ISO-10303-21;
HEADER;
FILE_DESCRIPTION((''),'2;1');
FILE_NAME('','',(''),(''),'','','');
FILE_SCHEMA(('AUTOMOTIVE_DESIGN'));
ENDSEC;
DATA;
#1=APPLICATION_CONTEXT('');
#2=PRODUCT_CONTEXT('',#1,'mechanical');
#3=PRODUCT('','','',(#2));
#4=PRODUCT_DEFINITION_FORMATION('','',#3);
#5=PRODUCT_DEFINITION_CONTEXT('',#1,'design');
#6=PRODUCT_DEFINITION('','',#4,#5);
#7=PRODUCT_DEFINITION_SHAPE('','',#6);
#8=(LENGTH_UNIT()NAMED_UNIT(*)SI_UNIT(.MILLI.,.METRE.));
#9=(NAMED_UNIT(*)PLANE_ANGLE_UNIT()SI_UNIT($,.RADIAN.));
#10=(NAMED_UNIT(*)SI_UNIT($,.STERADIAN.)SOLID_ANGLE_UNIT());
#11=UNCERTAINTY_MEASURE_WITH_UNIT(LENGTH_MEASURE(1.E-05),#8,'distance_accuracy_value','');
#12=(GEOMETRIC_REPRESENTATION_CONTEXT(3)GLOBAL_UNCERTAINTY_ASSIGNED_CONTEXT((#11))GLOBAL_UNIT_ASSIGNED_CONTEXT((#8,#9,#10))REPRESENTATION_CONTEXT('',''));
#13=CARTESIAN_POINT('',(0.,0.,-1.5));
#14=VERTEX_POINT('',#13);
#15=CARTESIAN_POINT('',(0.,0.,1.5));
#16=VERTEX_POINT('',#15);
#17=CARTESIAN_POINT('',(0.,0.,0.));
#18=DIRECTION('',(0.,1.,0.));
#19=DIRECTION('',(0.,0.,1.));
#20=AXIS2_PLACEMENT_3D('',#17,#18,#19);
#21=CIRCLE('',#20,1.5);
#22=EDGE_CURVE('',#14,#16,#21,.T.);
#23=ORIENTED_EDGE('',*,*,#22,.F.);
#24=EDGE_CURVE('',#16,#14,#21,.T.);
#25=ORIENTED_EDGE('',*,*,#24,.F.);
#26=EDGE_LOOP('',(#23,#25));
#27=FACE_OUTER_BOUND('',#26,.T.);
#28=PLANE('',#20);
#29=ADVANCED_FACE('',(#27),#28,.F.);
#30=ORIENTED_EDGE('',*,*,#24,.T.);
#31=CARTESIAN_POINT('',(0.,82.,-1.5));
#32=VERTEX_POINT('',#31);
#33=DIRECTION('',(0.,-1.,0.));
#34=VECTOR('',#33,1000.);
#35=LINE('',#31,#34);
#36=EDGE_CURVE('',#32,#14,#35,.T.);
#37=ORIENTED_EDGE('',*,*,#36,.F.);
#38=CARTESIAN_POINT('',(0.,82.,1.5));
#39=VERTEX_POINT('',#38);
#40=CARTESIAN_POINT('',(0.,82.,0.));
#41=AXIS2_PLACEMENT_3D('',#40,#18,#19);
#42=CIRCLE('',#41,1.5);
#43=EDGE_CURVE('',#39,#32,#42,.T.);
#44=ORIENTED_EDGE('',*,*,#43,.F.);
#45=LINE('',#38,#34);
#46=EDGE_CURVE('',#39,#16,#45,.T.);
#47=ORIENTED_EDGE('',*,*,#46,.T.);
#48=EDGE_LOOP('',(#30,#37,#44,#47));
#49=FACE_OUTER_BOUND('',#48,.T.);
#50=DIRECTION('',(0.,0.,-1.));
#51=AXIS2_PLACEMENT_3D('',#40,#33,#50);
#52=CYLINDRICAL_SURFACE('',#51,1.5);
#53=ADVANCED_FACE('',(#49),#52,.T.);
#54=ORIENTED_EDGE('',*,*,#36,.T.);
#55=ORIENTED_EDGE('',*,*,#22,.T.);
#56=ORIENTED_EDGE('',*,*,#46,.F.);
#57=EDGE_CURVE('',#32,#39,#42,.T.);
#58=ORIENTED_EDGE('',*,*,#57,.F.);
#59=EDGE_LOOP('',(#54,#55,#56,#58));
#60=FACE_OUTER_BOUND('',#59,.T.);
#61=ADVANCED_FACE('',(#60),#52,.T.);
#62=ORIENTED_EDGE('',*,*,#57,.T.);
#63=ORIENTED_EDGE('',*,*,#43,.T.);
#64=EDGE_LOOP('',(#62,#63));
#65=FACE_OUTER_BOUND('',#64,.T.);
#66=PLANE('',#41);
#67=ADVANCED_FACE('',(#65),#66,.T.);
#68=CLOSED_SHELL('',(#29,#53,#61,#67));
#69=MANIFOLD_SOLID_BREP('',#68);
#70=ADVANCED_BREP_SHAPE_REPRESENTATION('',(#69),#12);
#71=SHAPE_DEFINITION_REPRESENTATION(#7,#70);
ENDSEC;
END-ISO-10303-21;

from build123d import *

# Parameters (mm, degrees)
SKETCH1_R           = 1.5
BOSS_EXTRUDE1_DEPTH = 82


with BuildPart() as part:
    # Sketch1 → Boss-Extrude1 (new body)
    with BuildSketch(Plane(origin=(0, 0, 0), x_dir=(1, 0, 0), z_dir=(0, 1, 0))):
        with Locations(Location((0, 0, 0), (0, 0, 270))):
            Circle(SKETCH1_R)
    extrude(amount=BOSS_EXTRUDE1_DEPTH)


solid = part.part
